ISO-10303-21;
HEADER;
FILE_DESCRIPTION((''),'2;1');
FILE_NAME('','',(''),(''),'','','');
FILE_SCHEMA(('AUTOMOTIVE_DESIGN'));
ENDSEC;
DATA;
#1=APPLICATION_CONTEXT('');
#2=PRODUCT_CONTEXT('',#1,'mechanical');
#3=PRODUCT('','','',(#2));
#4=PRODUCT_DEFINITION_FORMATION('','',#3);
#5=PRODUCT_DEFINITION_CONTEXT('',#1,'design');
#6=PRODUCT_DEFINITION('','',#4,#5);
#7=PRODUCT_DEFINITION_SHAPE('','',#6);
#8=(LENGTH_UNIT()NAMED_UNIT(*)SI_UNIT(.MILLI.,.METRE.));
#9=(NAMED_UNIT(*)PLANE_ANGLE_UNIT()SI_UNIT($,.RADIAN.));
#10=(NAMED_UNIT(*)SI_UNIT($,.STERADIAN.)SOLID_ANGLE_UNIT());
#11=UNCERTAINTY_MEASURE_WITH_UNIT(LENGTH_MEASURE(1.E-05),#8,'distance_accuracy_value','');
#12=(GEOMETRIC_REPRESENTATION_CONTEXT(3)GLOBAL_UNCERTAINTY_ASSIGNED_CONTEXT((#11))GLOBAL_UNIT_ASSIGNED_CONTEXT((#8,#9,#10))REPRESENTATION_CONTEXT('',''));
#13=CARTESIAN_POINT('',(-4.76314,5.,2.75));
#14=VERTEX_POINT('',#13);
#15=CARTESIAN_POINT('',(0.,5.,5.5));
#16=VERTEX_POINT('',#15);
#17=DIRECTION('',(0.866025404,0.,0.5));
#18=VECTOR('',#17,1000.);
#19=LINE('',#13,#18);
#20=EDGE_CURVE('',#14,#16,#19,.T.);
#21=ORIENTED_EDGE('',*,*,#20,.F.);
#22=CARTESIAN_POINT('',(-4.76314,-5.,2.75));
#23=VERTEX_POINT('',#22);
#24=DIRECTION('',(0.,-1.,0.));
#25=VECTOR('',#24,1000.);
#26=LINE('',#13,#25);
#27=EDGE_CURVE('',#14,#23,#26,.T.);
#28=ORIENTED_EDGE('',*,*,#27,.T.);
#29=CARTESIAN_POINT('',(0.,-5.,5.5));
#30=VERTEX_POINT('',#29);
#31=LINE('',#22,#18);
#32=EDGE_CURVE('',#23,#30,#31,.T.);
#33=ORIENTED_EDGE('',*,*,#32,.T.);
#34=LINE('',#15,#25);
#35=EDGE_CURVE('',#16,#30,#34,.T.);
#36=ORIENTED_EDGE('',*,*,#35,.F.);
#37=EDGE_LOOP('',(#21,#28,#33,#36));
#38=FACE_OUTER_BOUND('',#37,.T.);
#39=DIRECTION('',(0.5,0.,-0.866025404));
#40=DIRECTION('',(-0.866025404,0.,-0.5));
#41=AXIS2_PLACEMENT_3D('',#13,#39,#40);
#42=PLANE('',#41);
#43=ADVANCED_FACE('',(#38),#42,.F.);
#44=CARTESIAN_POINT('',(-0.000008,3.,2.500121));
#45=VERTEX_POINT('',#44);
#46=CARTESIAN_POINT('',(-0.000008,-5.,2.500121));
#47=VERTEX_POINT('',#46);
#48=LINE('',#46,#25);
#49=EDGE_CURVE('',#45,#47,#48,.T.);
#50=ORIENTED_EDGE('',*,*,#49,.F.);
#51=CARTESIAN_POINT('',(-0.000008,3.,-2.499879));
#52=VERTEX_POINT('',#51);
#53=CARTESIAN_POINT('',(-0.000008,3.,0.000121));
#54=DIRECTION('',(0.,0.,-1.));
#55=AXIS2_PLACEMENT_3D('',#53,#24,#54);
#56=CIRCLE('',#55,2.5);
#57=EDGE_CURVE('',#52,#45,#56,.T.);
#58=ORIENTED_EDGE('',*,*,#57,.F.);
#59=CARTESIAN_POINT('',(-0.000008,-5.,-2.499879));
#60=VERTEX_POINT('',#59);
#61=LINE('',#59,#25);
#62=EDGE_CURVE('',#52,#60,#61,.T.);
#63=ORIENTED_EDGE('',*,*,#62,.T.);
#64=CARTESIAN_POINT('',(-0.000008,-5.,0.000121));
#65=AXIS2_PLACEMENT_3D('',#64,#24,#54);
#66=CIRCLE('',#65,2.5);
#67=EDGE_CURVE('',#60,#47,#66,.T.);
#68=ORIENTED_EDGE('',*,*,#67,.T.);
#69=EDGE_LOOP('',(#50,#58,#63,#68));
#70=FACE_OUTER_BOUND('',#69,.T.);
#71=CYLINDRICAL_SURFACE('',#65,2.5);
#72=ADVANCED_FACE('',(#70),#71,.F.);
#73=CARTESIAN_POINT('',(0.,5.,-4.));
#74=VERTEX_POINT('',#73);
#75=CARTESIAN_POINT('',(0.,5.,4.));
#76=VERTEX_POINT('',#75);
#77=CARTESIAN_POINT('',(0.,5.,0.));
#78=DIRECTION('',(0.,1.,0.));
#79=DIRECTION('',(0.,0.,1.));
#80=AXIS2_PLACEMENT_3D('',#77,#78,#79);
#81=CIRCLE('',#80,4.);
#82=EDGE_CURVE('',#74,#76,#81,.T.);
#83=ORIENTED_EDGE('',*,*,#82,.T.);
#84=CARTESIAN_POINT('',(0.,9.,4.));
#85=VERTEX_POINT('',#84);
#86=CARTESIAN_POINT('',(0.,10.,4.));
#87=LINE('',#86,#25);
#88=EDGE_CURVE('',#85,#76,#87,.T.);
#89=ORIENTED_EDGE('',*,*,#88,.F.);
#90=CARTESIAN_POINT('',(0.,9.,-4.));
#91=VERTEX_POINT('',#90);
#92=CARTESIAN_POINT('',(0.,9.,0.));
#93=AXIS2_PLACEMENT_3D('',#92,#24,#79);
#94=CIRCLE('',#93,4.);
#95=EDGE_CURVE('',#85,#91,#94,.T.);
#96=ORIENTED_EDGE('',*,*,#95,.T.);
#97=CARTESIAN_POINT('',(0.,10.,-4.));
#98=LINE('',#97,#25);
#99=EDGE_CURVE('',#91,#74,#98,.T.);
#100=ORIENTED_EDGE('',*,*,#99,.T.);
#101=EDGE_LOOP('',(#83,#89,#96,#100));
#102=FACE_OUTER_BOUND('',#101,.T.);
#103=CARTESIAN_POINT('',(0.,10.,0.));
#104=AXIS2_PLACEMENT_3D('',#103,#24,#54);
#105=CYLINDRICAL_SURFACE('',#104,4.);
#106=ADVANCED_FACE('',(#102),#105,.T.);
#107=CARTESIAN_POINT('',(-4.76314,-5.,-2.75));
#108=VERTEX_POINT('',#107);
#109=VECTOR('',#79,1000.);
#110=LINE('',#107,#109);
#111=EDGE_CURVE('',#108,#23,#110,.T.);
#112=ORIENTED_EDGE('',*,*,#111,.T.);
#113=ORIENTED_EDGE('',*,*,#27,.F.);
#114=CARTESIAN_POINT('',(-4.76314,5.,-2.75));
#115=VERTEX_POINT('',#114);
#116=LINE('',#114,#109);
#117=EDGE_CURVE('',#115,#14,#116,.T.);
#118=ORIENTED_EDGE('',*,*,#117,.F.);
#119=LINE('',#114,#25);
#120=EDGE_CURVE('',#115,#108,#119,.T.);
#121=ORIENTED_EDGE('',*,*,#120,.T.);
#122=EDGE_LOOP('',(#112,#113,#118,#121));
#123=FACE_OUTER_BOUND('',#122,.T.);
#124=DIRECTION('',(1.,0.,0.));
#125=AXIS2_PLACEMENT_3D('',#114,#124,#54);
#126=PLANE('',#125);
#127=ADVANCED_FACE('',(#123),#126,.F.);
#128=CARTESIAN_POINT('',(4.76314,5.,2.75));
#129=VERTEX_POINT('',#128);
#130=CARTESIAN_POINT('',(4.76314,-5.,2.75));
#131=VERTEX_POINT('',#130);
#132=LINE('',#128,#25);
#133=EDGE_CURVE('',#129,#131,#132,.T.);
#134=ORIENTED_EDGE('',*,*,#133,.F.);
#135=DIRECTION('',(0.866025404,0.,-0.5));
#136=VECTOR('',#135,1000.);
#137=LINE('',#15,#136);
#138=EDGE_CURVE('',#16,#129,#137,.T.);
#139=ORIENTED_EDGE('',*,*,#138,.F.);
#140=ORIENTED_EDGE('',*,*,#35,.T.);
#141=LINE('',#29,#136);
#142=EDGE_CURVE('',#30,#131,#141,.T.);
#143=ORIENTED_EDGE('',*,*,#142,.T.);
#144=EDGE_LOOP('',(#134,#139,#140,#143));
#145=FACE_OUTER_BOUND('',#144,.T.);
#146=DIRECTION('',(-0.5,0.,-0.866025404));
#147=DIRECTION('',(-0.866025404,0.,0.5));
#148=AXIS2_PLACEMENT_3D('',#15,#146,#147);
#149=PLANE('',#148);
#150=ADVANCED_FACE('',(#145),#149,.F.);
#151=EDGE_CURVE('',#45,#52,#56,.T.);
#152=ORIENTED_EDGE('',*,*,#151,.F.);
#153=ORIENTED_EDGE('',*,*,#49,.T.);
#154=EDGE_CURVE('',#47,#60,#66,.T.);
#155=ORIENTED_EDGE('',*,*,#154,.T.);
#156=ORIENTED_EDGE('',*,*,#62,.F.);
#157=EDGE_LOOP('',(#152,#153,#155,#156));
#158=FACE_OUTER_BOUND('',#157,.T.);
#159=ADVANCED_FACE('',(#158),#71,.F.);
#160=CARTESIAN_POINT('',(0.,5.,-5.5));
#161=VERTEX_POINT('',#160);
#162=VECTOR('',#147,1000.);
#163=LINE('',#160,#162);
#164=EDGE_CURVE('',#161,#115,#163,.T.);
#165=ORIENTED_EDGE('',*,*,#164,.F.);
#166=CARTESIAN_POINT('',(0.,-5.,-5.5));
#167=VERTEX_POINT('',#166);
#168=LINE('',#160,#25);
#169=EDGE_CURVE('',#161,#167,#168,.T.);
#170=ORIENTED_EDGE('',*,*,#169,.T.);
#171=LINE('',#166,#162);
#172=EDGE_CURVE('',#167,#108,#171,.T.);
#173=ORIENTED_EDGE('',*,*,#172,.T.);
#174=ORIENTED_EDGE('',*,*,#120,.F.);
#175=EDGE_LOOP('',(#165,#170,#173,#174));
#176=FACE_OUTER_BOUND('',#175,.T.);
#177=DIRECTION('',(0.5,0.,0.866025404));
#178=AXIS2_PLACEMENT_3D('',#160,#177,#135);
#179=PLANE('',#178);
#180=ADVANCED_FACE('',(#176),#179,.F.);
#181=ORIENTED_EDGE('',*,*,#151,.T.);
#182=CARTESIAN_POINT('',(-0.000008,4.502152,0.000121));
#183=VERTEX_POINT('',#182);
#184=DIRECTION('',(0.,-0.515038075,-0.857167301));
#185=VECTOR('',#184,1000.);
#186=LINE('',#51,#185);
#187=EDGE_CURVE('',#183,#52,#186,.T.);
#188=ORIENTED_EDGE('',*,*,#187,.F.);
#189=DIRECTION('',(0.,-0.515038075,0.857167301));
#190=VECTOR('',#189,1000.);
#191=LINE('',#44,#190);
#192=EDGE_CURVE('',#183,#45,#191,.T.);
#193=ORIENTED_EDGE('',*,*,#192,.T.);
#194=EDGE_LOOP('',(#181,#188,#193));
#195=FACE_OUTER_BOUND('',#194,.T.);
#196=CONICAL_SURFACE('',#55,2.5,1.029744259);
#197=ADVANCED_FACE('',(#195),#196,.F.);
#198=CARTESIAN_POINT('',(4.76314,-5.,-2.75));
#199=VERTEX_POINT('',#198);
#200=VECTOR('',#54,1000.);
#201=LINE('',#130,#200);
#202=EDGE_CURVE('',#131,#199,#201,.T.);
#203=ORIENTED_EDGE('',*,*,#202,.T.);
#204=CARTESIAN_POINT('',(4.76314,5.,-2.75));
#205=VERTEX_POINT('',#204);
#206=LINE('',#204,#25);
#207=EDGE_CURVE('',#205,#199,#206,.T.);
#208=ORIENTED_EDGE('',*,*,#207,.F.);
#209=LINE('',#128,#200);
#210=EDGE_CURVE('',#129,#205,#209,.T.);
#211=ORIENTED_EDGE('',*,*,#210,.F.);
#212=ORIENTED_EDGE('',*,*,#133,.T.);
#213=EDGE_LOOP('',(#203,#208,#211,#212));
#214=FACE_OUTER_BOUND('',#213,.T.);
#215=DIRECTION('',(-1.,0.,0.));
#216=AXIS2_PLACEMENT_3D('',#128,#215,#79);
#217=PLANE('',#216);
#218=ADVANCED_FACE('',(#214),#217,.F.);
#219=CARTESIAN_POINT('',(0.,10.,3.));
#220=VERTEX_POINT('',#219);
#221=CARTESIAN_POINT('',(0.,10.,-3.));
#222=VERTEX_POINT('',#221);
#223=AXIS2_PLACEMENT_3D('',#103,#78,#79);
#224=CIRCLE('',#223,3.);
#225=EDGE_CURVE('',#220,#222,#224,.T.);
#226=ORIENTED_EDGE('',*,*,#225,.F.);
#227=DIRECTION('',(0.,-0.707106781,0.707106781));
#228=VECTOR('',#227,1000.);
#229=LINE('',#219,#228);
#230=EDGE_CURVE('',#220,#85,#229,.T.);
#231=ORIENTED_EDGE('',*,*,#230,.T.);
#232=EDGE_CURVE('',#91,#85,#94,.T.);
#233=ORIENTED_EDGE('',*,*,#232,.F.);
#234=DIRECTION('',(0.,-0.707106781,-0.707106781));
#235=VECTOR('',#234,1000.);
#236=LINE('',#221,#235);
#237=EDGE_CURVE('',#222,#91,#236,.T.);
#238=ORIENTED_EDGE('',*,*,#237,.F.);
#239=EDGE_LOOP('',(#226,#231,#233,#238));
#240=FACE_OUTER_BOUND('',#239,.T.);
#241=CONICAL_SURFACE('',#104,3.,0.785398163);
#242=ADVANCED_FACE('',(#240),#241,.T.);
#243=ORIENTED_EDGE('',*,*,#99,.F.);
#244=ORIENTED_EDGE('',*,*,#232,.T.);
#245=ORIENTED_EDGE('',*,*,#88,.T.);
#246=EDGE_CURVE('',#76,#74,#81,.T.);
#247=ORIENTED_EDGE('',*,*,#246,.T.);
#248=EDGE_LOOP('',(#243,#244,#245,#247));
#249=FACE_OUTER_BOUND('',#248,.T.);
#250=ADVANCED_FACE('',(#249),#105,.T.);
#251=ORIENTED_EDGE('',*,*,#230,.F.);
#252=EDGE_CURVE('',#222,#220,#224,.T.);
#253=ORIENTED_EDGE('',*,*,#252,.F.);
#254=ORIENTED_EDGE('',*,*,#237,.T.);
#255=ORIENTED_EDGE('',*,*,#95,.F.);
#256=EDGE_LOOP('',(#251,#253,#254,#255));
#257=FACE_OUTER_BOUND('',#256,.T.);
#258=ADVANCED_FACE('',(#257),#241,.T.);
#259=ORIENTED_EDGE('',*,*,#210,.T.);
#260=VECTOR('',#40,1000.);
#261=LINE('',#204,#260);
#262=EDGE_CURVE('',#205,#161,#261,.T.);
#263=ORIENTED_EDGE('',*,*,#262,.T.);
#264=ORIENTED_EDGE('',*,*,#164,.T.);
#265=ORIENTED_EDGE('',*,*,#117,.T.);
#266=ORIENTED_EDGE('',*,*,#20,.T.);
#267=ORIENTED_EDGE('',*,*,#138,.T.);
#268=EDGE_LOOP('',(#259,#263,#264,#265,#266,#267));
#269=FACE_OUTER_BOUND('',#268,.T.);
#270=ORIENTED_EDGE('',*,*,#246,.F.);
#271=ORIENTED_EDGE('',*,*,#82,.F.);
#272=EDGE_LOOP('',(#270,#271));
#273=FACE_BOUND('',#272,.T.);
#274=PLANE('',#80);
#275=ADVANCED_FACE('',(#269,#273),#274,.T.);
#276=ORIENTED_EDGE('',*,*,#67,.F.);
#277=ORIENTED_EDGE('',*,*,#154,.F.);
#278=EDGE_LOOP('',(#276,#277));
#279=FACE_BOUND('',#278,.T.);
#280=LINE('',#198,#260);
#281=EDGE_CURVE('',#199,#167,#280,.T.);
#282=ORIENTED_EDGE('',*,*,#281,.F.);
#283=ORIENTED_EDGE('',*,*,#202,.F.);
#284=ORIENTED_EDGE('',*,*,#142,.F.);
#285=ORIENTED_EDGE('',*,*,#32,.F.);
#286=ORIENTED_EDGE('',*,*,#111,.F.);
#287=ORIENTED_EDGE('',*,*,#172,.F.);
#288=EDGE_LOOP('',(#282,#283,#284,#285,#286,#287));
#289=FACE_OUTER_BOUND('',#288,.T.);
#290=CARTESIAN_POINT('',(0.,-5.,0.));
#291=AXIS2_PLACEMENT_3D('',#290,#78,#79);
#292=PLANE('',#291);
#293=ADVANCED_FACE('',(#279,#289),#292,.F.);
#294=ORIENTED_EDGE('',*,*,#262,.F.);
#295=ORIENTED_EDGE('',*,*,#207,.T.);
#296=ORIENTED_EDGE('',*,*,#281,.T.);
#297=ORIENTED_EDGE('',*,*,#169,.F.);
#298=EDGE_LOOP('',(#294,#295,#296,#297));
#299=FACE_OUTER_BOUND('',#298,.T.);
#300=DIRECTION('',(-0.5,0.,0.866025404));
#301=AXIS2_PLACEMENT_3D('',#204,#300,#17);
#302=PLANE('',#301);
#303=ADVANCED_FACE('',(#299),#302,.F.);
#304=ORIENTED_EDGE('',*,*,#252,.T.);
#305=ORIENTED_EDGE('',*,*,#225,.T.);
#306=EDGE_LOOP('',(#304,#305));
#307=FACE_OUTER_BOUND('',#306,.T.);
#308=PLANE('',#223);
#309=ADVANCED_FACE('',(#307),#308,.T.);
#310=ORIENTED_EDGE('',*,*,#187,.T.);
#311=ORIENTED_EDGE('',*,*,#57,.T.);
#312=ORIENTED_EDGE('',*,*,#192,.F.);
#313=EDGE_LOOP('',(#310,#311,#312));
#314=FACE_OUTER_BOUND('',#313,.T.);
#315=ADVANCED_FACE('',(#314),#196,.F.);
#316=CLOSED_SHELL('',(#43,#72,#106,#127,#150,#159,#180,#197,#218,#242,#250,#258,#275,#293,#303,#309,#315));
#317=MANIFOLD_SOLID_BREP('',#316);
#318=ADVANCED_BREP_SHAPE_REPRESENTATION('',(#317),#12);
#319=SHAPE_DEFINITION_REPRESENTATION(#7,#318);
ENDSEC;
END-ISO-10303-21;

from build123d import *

# Parameters (mm, degrees)
BOSS_EXTRUDE1_DEPTH            = 5
SKETCH3_R                      = 4
BOSS_EXTRUDE2_DEPTH            = 5
CHAMFER1_SIZE                  = 1
M6X1_0_TAPPED_HOLE2_AT_2_COUNT = 2
M6X1_0_TAPPED_HOLE2_AT_2_PITCH = 0.000121298


with BuildPart() as part:
    # Sketch1 → Boss-Extrude1 (new, symmetric)
    with BuildSketch(Plane(origin=(0, 0, 0), x_dir=(1, 0, 0), z_dir=(0, 1, 0))):
        Polygon((0, 5.5), (-4.763139721, 2.75), (-4.763139721, -2.75), (0, -5.5), (4.763139721, -2.75), (4.763139721, 2.75), align=None)
    extrude(amount=BOSS_EXTRUDE1_DEPTH, both=True)

    # Sketch3 → Boss-Extrude2 (add)
    with BuildSketch(Plane(origin=(0, 5, 0), x_dir=(1, 0, 0), z_dir=(0, 1, 0))):
        with Locations(Location((0, 0, 0), (0, 0, 270))):
            Circle(SKETCH3_R)
    extrude(amount=BOSS_EXTRUDE2_DEPTH)

    # Chamfer1
    chamfer1_edges = [part.edges().sort_by_distance(p)[0] for p in [
        (0, 10, -4),
    ]]
    chamfer(chamfer1_edges, length=CHAMFER1_SIZE)

    # Sketch19 → M6x1.0 Tapped Hole2 (revolve, cut)
    with BuildSketch(Plane(origin=(-7.813e-06, -5, 0.000121047), x_dir=(0, 0, -1), z_dir=(1, 0, 0))):
        Polygon((0, 0), (0, 9.502151548), (2.5, 8), (2.5, 0), align=None)
    m6x1_0_tapped_hole2 = revolve(axis=Axis((-7.813e-06, -11.35, 0.000121047), (0, 1, 0)), mode=Mode.SUBTRACT)

    # M6x1.0 Tapped Hole2 at 2: M6x1.0 Tapped Hole2 ×2
    with Locations(*[Vector(0.06441225047789163, 0, -0.9979233748080929) * (i * M6X1_0_TAPPED_HOLE2_AT_2_PITCH) for i in range(1, M6X1_0_TAPPED_HOLE2_AT_2_COUNT)]):
        add(m6x1_0_tapped_hole2, mode=Mode.SUBTRACT)


solid = part.part
